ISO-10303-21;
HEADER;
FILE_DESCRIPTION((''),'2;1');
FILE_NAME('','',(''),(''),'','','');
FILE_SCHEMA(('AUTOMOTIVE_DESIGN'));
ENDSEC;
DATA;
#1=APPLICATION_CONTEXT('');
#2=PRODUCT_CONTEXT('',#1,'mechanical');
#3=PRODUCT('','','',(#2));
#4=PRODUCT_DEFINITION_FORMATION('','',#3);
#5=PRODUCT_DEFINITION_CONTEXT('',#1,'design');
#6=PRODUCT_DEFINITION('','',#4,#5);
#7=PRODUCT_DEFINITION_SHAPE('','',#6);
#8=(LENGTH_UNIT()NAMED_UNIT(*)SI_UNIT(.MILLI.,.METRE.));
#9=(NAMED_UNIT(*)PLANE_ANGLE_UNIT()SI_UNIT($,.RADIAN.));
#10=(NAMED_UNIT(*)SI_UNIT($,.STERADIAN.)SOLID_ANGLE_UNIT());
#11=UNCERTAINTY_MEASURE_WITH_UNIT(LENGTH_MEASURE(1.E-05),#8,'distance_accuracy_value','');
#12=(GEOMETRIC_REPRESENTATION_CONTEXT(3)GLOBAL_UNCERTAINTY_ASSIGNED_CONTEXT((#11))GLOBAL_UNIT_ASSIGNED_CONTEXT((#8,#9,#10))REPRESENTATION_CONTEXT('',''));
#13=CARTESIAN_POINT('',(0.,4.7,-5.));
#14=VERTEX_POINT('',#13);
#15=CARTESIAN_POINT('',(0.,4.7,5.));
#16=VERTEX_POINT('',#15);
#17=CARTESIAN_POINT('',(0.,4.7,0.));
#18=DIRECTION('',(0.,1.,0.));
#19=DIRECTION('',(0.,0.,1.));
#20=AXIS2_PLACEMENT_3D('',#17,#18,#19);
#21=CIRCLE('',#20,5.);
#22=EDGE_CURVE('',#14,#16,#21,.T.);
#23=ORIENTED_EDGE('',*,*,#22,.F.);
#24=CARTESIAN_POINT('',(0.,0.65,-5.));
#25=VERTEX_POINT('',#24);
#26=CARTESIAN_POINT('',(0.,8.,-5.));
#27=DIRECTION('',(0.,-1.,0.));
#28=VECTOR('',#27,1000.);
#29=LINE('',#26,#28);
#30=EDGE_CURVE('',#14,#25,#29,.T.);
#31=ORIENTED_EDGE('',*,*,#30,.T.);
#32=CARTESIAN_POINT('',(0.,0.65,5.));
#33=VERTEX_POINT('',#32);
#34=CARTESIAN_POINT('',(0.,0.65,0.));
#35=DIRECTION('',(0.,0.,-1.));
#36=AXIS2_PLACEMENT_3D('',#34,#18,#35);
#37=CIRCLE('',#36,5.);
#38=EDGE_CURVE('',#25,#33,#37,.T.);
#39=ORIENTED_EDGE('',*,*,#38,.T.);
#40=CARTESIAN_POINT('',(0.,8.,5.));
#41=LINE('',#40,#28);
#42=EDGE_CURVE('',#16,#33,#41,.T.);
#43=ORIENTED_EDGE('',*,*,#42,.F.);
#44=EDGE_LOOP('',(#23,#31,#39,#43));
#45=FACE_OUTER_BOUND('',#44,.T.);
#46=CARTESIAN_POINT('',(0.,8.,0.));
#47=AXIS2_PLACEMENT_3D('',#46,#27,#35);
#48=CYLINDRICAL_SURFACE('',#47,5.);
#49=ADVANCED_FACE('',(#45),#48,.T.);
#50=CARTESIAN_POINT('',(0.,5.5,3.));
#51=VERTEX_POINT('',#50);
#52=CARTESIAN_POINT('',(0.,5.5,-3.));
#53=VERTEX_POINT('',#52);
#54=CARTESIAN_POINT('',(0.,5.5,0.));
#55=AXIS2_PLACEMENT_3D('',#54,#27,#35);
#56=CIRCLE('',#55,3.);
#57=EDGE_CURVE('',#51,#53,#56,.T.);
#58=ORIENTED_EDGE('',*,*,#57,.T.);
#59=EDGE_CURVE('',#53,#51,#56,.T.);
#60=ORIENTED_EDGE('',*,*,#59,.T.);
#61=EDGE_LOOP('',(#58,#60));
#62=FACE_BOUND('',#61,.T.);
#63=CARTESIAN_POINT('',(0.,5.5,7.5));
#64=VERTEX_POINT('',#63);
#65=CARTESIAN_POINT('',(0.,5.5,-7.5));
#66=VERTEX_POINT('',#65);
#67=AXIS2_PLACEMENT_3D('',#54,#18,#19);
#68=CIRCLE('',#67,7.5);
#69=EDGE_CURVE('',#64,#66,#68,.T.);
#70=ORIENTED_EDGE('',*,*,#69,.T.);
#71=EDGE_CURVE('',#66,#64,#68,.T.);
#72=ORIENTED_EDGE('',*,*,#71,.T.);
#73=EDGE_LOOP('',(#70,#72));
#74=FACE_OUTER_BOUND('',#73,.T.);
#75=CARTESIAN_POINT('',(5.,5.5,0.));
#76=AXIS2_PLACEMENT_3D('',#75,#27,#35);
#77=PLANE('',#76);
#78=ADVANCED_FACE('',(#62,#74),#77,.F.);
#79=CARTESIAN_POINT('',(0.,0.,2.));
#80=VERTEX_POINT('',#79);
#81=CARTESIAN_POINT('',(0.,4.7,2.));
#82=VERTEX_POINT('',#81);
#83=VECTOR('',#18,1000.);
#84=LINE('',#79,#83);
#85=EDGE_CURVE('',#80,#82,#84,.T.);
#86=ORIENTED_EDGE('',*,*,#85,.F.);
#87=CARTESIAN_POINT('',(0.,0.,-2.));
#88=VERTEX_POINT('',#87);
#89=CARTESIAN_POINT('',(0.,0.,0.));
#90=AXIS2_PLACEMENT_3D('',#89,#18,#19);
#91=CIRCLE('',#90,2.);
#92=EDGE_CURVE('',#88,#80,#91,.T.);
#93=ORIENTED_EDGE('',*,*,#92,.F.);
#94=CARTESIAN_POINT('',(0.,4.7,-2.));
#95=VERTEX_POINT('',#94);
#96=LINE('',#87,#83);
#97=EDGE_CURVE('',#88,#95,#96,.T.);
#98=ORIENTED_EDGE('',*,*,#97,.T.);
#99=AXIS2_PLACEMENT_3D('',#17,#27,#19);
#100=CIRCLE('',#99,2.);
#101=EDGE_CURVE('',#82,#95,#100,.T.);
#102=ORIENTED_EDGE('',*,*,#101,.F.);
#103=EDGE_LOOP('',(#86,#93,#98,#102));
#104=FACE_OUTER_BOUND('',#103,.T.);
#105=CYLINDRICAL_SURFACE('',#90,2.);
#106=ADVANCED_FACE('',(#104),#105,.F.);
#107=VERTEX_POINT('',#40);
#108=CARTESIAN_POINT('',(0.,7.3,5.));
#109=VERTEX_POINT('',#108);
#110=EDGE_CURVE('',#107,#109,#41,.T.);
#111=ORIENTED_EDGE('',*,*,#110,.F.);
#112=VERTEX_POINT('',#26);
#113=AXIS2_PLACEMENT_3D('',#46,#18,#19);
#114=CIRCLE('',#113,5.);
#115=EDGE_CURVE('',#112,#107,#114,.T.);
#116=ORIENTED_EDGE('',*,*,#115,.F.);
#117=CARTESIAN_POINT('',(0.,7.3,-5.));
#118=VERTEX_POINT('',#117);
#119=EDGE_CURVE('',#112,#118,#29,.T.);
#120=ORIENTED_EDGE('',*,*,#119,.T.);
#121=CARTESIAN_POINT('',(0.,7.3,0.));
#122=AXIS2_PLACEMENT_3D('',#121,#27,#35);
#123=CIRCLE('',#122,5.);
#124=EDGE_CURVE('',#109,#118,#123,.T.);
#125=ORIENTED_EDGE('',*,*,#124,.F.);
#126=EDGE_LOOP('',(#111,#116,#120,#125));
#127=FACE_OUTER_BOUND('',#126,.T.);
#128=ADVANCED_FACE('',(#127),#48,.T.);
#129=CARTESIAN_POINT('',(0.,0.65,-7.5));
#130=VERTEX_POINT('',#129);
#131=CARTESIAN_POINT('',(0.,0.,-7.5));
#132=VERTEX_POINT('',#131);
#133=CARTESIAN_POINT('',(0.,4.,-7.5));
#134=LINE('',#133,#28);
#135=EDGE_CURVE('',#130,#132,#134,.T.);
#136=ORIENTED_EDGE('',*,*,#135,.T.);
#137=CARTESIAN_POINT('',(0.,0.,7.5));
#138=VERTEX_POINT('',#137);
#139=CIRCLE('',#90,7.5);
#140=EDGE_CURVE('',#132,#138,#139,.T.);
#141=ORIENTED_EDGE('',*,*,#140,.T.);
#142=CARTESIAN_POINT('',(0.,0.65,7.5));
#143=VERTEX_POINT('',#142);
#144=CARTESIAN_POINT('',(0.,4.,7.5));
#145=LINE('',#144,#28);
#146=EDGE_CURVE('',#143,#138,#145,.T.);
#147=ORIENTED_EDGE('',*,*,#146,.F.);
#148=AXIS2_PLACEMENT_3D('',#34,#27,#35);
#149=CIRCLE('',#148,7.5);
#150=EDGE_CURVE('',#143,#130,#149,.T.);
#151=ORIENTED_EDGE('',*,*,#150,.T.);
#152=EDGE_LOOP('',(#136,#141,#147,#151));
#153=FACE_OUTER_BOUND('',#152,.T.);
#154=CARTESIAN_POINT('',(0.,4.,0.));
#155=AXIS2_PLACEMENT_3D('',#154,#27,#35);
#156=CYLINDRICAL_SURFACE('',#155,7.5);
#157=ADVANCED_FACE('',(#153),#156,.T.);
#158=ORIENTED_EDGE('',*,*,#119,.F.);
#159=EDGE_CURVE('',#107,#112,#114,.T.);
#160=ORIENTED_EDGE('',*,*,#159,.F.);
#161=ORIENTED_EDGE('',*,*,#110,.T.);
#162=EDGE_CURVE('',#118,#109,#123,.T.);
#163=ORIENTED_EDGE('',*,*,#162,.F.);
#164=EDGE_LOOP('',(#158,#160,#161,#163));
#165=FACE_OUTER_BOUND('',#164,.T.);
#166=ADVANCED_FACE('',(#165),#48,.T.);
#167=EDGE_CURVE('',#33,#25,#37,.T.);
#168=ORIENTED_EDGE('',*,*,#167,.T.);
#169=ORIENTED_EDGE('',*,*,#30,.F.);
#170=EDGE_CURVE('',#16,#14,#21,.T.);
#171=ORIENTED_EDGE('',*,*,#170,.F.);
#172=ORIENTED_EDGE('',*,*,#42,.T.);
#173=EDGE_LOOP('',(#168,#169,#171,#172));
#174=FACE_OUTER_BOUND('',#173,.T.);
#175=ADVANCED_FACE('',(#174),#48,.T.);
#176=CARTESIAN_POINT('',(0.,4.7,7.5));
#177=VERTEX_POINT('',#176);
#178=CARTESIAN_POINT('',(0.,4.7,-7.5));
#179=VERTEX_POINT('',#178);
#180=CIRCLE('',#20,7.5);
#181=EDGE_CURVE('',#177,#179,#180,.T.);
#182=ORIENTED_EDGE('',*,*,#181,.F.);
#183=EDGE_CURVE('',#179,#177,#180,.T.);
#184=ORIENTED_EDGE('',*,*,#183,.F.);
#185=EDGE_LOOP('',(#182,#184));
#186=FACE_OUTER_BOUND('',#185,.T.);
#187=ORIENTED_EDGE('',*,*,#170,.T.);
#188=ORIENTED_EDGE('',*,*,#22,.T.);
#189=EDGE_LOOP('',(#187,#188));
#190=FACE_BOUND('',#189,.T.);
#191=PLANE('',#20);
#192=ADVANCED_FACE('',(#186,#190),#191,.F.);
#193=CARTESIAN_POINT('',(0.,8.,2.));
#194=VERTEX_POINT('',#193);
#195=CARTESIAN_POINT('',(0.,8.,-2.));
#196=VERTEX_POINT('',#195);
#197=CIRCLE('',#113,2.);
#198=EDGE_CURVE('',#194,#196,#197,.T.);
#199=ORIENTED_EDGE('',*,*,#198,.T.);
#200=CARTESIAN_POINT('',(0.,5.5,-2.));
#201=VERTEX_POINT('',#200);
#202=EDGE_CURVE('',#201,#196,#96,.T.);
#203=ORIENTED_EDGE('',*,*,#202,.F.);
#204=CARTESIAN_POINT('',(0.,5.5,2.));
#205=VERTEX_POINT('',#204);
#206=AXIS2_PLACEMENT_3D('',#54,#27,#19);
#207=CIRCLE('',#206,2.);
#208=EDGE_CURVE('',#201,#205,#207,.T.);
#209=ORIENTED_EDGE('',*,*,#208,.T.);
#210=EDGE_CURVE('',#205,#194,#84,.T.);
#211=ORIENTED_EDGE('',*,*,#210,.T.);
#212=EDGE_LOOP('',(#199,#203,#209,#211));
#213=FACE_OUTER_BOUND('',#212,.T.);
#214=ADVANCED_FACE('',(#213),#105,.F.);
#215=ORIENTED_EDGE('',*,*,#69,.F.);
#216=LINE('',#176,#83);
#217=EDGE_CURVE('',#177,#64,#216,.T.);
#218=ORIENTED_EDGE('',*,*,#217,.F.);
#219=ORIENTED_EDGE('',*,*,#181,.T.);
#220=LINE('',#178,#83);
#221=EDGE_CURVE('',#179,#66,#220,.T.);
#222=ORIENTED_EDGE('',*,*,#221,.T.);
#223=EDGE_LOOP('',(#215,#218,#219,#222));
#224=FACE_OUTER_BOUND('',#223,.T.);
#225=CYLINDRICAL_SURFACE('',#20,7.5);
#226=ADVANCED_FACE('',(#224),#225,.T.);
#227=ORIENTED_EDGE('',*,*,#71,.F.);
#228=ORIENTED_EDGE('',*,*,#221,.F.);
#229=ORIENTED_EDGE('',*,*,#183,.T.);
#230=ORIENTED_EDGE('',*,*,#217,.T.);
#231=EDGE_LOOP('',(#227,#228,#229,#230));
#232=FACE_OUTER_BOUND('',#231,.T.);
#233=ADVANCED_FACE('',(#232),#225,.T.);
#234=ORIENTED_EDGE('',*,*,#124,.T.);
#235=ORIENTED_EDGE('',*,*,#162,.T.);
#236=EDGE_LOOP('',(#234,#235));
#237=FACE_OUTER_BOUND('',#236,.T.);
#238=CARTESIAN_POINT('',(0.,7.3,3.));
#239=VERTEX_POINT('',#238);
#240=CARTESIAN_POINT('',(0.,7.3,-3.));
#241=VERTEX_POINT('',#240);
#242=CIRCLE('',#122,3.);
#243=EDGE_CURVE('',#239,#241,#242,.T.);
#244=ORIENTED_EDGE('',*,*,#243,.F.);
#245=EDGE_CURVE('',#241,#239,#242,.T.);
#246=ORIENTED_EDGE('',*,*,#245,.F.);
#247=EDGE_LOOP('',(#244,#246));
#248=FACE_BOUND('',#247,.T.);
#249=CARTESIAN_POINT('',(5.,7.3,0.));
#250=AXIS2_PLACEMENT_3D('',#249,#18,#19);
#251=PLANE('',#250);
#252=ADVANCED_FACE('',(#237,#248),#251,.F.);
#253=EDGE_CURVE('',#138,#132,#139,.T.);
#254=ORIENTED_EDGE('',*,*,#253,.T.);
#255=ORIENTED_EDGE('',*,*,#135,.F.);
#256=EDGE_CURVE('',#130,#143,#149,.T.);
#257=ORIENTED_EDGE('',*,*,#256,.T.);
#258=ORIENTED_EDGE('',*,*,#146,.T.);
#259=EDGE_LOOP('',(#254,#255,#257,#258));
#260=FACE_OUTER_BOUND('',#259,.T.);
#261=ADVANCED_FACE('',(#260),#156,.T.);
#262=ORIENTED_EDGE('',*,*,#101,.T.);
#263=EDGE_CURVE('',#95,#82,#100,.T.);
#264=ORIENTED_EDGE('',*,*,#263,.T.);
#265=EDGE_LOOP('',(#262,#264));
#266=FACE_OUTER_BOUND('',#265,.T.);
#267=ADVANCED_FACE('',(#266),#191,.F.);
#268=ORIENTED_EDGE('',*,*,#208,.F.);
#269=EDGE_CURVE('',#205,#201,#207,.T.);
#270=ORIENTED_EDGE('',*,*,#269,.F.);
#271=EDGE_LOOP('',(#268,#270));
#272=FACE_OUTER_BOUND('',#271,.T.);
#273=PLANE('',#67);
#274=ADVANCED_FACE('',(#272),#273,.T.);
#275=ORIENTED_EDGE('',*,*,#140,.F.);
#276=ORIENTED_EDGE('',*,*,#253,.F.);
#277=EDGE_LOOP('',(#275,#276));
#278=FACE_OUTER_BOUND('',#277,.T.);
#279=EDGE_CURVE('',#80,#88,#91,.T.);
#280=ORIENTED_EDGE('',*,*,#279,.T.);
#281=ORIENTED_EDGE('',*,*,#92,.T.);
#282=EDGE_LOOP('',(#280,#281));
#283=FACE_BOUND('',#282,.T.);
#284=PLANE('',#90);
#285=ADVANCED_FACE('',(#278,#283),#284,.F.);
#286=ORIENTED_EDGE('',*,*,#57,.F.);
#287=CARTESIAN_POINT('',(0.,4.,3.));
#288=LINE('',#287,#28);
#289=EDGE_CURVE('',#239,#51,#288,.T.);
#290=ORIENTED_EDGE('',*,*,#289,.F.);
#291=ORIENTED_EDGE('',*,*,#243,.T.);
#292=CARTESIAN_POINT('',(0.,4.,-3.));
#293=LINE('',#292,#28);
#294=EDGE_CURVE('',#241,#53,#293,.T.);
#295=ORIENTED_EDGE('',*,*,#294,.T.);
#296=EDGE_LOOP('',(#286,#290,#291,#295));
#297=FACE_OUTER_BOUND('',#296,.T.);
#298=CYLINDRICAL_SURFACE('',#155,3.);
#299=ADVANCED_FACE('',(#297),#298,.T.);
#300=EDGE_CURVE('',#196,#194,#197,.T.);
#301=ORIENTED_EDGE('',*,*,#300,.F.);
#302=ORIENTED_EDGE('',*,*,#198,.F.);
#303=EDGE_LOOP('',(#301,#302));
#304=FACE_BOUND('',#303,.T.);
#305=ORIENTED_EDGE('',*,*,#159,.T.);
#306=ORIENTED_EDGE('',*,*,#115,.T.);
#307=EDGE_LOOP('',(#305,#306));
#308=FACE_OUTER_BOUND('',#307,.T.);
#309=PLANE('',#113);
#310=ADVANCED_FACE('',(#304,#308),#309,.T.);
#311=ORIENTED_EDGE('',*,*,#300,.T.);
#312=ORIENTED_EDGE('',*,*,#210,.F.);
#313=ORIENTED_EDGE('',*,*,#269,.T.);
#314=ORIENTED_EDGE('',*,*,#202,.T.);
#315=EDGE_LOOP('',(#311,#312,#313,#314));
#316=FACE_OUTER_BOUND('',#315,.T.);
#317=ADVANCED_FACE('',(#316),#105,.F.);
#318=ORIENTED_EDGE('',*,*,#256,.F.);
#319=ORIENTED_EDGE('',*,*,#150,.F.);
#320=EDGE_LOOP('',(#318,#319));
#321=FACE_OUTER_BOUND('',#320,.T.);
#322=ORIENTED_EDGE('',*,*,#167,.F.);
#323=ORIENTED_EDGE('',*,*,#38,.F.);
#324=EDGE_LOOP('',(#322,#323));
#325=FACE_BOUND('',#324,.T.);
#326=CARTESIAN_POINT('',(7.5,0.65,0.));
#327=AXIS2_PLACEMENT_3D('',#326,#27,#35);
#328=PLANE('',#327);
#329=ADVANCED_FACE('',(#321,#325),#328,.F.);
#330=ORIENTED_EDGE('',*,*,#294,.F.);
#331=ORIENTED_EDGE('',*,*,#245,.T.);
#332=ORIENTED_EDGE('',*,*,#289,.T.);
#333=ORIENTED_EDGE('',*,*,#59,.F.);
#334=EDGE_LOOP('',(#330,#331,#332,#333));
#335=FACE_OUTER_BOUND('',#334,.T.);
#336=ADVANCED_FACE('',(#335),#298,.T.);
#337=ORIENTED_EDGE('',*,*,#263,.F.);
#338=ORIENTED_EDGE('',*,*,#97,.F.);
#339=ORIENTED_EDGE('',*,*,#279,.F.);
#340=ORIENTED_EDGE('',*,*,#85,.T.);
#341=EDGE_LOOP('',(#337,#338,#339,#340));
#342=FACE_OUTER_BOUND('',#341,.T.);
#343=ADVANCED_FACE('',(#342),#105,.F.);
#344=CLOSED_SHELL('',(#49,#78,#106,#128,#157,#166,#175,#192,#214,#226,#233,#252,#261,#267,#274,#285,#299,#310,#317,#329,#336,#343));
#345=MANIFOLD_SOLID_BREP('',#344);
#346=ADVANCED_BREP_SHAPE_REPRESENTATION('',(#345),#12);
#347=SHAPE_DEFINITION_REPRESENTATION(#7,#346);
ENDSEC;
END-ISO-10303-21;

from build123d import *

# Parameters (mm, degrees)
SKETCH1_R           = 7.5
BOSS_EXTRUDE1_DEPTH = 4
SKETCH3_W           = 3
SKETCH3_H           = 3.25
SKETCH4_R           = 5
BOSS_EXTRUDE2_DEPTH = 8
SKETCH5_W           = 2
SKETCH5_H           = 1.8
SKETCH6_R           = 2
CUT_EXTRUDE1_DEPTH  = 14.285330256
CUT_EXTRUDE3_START  = -2
SKETCH7_R           = 8.572097994
SKETCH7_R_2         = 5
CUT_EXTRUDE3_DEPTH  = 2
BOSS_EXTRUDE3_START = -0.8
SKETCH8_R           = 7.5
BOSS_EXTRUDE3_DEPTH = 0.8


with BuildPart() as part:
    # Sketch1 → Boss-Extrude1 (new body)
    with BuildSketch(Plane(origin=(0, 0, 0), x_dir=(1, 0, 0), z_dir=(0, 1, 0))):
        with Locations(Location((0, 0, 0), (0, 0, 270))):
            Circle(SKETCH1_R)
    extrude(amount=BOSS_EXTRUDE1_DEPTH)

    # Sketch3 → Cut-Revolve1 (revolve, cut)
    with BuildSketch(Plane.XY, mode=Mode.PRIVATE) as cut_revolve1_sk:
        with Locations((6, 2.275)):
            Rectangle(SKETCH3_W, SKETCH3_H)
    revolve(cut_revolve1_sk.sketch.rotate(Axis((0, 0, 0), (0, 1, 0)), 90), axis=Axis((0, 0, 0), (0, 1, 0)), mode=Mode.SUBTRACT)

    # Sketch4 → Boss-Extrude2 (add)
    with BuildSketch(Plane(origin=(0, 0, 0), x_dir=(1, 0, 0), z_dir=(0, 1, 0))):
        with Locations(Location((0, 0, 0), (0, 0, 90))):
            Circle(SKETCH4_R)
    extrude(amount=BOSS_EXTRUDE2_DEPTH)

    # Sketch5 → Cut-Revolve2 (revolve, cut)
    with BuildSketch(Plane.XY, mode=Mode.PRIVATE) as cut_revolve2_sk:
        with Locations((4, 6.4)):
            Rectangle(SKETCH5_W, SKETCH5_H)
    revolve(cut_revolve2_sk.sketch.rotate(Axis((0, 4, 0), (0, 1, 0)), 90), axis=Axis((0, 4, 0), (0, 1, 0)), mode=Mode.SUBTRACT)

    # Sketch6 → Cut-Extrude1 (cut, through all)
    with BuildSketch(Plane(origin=(0, 8, 0), x_dir=(1, 0, 0), z_dir=(0, 1, 0))):
        with Locations(Location((0, 0, 0), (0, 0, 270))):
            Circle(SKETCH6_R)
    extrude(amount=-CUT_EXTRUDE1_DEPTH, mode=Mode.SUBTRACT)

    # Sketch7 → Cut-Extrude3 (cut)
    with BuildSketch(Plane(origin=(0, 4, 0), x_dir=(1, 0, 0), z_dir=(0, 1, 0)).offset(CUT_EXTRUDE3_START)):
        Circle(SKETCH7_R)
        with Locations(Location((0, 0, 0), (0, 0, 90))):
            Circle(SKETCH7_R_2, mode=Mode.SUBTRACT)
    extrude(amount=CUT_EXTRUDE3_DEPTH, mode=Mode.SUBTRACT)

    # Sketch8 → Boss-Extrude3 (add)
    with BuildSketch(Plane(origin=(0, 5.5, 0), x_dir=(1, 0, 0), z_dir=(0, 1, 0)).offset(BOSS_EXTRUDE3_START)):
        with Locations(Location((0, 0, 0), (0, 0, 270))):
            Circle(SKETCH8_R)
    extrude(amount=BOSS_EXTRUDE3_DEPTH)


solid = part.part
